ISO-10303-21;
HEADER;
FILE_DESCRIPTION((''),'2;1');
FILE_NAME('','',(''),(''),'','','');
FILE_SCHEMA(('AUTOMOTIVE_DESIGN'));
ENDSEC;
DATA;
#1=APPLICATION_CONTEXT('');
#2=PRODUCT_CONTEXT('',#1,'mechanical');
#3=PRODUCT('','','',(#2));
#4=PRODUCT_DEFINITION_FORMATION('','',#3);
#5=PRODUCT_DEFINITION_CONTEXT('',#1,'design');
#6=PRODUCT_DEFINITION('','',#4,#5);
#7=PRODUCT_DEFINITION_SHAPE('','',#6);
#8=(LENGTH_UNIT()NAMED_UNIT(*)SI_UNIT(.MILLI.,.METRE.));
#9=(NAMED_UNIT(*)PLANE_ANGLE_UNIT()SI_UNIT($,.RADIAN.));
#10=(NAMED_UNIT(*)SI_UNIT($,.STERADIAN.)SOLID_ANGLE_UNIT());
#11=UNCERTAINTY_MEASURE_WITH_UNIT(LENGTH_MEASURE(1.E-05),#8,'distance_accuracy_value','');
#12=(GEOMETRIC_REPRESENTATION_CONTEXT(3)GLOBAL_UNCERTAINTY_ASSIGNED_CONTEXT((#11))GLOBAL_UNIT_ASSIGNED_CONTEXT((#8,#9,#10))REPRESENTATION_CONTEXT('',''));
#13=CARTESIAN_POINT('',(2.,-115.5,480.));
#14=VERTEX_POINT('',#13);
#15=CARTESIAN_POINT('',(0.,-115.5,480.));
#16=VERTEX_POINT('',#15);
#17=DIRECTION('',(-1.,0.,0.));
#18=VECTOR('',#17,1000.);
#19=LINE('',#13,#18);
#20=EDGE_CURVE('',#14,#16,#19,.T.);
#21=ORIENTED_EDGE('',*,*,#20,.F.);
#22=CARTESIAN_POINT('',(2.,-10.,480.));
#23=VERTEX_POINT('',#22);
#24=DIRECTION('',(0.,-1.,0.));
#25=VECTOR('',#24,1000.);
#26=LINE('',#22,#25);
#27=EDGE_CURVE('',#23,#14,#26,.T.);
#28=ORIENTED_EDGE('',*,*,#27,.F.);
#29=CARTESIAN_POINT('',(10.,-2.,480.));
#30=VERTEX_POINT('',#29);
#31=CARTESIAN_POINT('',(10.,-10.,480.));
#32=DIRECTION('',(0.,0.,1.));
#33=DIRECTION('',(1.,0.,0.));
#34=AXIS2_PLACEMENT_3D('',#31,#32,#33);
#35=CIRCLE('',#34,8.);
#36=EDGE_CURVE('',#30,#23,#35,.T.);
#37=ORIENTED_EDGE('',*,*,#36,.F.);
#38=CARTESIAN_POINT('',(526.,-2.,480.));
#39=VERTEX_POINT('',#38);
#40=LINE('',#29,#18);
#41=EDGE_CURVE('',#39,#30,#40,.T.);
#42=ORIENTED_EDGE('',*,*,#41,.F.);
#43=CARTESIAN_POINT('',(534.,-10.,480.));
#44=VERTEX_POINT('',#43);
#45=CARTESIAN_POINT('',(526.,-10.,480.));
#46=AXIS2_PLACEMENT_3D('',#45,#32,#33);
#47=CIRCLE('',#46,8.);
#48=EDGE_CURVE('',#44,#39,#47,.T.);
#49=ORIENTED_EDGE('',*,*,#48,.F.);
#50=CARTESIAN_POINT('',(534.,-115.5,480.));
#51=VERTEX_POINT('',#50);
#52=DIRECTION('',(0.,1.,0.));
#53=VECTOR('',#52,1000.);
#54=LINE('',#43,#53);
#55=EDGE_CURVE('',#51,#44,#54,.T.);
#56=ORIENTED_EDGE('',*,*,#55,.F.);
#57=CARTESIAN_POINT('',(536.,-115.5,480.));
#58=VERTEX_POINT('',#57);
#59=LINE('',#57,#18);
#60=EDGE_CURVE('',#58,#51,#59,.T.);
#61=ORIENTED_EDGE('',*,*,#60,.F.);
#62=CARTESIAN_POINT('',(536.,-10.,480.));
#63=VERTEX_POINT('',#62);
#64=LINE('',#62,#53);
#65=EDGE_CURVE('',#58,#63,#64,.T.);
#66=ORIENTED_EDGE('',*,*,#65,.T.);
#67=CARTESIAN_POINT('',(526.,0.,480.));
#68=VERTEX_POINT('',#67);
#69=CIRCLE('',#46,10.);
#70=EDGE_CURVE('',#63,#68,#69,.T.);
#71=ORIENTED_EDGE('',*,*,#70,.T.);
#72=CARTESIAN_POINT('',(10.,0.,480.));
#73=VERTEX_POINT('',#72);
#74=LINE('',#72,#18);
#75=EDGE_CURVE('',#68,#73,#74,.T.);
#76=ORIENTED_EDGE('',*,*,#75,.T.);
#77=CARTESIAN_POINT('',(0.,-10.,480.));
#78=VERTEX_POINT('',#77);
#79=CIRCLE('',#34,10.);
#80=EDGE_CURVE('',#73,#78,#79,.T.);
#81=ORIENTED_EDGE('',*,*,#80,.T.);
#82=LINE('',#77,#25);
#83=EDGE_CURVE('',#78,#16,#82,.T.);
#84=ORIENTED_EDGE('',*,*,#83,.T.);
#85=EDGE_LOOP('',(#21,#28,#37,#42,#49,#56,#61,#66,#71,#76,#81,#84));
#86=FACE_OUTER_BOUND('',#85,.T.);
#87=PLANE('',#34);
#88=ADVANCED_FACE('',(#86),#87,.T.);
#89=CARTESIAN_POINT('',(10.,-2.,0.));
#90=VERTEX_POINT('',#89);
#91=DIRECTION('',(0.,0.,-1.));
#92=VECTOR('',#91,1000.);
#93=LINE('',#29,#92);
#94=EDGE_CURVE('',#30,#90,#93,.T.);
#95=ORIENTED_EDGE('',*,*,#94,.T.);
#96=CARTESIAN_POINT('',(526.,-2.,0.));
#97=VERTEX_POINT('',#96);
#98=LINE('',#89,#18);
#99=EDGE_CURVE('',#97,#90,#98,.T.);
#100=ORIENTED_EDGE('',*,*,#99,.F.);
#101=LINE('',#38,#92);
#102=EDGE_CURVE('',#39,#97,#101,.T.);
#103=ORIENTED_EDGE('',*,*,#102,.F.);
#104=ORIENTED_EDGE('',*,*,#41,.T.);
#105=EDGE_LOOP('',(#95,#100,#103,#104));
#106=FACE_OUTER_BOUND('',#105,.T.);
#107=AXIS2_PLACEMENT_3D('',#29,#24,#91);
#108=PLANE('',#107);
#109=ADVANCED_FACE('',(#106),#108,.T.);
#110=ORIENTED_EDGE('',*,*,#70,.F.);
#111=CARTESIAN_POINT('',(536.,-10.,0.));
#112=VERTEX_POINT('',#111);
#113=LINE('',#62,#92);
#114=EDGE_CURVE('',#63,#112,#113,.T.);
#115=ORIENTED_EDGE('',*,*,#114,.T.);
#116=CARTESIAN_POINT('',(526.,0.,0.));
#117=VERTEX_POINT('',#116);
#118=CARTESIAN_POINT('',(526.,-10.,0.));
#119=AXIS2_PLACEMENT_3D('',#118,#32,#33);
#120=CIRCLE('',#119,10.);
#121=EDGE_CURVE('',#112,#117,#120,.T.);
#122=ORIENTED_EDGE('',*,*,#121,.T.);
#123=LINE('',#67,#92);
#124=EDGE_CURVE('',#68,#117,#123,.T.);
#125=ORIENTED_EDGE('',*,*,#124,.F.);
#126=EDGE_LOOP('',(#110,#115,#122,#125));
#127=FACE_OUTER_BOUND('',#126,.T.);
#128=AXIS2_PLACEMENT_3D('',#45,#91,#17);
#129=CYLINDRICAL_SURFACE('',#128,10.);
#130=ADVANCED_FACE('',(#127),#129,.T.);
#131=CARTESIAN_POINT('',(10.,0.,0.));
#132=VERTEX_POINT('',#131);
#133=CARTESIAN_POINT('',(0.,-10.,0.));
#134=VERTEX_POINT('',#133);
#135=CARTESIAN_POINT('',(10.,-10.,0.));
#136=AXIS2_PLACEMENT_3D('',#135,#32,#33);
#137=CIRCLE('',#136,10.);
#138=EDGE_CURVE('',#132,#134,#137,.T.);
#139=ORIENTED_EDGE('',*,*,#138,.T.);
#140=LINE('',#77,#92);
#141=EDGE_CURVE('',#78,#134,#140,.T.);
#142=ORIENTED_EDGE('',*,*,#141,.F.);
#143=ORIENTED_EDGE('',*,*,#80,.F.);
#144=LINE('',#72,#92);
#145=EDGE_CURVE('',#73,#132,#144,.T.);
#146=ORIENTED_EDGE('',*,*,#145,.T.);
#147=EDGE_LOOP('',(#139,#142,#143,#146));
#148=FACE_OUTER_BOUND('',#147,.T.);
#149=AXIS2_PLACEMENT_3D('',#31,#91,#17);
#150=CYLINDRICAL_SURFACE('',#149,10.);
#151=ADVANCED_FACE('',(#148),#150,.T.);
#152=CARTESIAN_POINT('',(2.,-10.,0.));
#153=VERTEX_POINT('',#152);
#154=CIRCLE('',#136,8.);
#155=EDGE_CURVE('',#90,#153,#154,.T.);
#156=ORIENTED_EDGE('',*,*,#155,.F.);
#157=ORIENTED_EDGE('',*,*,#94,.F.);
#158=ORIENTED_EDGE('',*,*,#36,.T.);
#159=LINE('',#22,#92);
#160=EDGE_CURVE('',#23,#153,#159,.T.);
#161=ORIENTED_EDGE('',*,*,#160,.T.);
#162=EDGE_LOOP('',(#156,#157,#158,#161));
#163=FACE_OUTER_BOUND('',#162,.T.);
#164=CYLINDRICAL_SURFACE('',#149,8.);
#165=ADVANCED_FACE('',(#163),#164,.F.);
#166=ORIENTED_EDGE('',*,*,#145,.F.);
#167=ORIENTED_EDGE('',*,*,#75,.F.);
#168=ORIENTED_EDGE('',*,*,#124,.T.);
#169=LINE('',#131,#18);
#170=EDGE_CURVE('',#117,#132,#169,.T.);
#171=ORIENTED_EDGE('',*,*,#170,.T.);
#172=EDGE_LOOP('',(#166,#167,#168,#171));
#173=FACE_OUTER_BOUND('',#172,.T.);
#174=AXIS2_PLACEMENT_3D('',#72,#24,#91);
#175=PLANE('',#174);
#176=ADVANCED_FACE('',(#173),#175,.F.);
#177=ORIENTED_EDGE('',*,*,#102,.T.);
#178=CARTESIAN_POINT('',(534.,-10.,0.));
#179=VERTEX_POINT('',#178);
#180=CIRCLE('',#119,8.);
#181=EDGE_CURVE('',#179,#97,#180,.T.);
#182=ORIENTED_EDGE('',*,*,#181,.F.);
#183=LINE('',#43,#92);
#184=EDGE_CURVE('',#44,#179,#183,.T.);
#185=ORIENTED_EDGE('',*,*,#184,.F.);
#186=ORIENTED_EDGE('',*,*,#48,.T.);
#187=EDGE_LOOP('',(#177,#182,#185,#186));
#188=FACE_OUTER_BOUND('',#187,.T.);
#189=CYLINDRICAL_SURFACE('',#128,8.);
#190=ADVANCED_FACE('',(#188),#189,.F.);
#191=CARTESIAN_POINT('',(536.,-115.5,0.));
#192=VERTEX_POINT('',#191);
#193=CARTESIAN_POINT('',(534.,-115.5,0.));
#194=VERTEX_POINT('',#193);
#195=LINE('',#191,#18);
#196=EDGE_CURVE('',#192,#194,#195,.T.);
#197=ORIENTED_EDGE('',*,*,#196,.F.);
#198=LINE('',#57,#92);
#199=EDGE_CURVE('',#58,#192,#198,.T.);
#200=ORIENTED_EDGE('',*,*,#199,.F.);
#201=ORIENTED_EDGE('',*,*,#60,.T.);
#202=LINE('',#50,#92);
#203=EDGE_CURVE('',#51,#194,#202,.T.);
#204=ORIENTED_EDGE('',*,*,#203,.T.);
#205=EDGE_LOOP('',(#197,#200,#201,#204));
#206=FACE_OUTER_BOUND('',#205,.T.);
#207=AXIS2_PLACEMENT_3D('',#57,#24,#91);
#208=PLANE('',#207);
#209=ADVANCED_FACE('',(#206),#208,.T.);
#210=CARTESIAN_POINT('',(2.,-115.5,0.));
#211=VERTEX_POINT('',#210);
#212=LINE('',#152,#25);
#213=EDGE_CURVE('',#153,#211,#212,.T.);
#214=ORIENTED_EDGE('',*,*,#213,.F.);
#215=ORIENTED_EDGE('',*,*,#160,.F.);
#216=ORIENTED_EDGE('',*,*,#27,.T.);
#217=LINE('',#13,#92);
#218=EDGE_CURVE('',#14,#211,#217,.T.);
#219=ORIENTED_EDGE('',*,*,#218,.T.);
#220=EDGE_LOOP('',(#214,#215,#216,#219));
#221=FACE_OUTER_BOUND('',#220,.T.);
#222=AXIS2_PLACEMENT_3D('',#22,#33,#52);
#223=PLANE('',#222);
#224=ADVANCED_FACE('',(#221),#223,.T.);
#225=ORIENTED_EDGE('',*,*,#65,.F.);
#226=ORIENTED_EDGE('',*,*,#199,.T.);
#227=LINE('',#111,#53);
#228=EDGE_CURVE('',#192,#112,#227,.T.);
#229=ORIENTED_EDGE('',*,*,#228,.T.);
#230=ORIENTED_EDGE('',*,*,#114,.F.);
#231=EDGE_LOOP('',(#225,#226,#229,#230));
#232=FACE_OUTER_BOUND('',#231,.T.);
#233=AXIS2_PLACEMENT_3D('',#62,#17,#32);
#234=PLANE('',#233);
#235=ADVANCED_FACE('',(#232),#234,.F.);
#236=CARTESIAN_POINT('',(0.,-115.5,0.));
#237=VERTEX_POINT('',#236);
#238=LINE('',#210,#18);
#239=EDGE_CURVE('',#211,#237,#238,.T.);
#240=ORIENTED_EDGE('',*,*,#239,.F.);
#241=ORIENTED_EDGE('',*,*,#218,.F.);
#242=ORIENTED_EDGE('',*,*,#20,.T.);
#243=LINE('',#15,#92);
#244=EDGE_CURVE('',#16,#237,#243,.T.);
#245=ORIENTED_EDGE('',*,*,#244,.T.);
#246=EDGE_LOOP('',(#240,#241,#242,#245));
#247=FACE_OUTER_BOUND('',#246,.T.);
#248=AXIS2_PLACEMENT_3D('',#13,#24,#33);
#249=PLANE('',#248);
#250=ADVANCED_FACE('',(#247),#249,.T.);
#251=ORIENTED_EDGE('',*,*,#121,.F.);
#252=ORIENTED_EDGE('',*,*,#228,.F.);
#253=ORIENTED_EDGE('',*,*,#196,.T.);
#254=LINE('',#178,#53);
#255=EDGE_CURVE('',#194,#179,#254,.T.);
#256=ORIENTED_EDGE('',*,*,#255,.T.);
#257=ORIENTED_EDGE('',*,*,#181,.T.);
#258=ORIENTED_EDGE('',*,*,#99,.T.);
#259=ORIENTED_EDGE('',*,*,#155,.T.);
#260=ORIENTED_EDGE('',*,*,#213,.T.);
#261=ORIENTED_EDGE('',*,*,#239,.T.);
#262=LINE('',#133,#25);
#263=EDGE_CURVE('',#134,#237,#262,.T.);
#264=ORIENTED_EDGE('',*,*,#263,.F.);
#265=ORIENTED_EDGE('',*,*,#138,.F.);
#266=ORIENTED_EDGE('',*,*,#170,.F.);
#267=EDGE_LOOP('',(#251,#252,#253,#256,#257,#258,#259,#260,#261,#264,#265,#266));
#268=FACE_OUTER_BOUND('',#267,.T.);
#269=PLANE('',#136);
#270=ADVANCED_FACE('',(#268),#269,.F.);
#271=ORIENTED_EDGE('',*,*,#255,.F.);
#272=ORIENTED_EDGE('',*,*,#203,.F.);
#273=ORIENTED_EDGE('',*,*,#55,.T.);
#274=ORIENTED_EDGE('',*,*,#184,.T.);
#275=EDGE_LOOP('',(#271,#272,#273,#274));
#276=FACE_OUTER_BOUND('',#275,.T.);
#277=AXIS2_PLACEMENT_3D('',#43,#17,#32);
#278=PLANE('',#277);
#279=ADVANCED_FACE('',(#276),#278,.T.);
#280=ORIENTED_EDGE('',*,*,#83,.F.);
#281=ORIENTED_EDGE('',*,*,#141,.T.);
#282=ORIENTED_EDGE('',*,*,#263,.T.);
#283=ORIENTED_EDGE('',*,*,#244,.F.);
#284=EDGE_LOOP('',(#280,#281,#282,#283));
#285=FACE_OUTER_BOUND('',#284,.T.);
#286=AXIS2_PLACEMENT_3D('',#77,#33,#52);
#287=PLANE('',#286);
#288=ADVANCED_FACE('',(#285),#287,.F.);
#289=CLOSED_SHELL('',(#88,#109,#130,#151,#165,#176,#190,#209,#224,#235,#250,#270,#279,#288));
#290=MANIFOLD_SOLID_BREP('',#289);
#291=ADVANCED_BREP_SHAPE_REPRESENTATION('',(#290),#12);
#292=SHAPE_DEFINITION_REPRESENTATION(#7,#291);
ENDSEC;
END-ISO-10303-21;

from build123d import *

# Parameters (mm, degrees)
EXTRUDE_THIN1_DEPTH = 480


with BuildPart() as part:
    # Sketch1 → Extrude-Thin1 (new body)
    with BuildSketch(Plane.XY):
        with BuildLine():
            Line((0, -115.5), (0, -10))
            ThreePointArc((0, -10), (2.928932188, -2.928932188), (10, 0))
            Line((10, 0), (526, 0))
            ThreePointArc((526, 0), (533.071067812, -2.928932188), (536, -10))
            Line((536, -10), (536, -115.5))
            Line((536, -115.5), (534, -115.5))
            Line((534, -115.5), (534, -10))
            ThreePointArc((534, -10), (531.656854249, -4.343145751), (526, -2))
            Line((526, -2), (10, -2))
            ThreePointArc((10, -2), (4.343145751, -4.343145751), (2, -10))
            Line((2, -10), (2, -115.5))
            Line((2, -115.5), (0, -115.5))
        make_face()
    extrude(amount=EXTRUDE_THIN1_DEPTH)


solid = part.part
